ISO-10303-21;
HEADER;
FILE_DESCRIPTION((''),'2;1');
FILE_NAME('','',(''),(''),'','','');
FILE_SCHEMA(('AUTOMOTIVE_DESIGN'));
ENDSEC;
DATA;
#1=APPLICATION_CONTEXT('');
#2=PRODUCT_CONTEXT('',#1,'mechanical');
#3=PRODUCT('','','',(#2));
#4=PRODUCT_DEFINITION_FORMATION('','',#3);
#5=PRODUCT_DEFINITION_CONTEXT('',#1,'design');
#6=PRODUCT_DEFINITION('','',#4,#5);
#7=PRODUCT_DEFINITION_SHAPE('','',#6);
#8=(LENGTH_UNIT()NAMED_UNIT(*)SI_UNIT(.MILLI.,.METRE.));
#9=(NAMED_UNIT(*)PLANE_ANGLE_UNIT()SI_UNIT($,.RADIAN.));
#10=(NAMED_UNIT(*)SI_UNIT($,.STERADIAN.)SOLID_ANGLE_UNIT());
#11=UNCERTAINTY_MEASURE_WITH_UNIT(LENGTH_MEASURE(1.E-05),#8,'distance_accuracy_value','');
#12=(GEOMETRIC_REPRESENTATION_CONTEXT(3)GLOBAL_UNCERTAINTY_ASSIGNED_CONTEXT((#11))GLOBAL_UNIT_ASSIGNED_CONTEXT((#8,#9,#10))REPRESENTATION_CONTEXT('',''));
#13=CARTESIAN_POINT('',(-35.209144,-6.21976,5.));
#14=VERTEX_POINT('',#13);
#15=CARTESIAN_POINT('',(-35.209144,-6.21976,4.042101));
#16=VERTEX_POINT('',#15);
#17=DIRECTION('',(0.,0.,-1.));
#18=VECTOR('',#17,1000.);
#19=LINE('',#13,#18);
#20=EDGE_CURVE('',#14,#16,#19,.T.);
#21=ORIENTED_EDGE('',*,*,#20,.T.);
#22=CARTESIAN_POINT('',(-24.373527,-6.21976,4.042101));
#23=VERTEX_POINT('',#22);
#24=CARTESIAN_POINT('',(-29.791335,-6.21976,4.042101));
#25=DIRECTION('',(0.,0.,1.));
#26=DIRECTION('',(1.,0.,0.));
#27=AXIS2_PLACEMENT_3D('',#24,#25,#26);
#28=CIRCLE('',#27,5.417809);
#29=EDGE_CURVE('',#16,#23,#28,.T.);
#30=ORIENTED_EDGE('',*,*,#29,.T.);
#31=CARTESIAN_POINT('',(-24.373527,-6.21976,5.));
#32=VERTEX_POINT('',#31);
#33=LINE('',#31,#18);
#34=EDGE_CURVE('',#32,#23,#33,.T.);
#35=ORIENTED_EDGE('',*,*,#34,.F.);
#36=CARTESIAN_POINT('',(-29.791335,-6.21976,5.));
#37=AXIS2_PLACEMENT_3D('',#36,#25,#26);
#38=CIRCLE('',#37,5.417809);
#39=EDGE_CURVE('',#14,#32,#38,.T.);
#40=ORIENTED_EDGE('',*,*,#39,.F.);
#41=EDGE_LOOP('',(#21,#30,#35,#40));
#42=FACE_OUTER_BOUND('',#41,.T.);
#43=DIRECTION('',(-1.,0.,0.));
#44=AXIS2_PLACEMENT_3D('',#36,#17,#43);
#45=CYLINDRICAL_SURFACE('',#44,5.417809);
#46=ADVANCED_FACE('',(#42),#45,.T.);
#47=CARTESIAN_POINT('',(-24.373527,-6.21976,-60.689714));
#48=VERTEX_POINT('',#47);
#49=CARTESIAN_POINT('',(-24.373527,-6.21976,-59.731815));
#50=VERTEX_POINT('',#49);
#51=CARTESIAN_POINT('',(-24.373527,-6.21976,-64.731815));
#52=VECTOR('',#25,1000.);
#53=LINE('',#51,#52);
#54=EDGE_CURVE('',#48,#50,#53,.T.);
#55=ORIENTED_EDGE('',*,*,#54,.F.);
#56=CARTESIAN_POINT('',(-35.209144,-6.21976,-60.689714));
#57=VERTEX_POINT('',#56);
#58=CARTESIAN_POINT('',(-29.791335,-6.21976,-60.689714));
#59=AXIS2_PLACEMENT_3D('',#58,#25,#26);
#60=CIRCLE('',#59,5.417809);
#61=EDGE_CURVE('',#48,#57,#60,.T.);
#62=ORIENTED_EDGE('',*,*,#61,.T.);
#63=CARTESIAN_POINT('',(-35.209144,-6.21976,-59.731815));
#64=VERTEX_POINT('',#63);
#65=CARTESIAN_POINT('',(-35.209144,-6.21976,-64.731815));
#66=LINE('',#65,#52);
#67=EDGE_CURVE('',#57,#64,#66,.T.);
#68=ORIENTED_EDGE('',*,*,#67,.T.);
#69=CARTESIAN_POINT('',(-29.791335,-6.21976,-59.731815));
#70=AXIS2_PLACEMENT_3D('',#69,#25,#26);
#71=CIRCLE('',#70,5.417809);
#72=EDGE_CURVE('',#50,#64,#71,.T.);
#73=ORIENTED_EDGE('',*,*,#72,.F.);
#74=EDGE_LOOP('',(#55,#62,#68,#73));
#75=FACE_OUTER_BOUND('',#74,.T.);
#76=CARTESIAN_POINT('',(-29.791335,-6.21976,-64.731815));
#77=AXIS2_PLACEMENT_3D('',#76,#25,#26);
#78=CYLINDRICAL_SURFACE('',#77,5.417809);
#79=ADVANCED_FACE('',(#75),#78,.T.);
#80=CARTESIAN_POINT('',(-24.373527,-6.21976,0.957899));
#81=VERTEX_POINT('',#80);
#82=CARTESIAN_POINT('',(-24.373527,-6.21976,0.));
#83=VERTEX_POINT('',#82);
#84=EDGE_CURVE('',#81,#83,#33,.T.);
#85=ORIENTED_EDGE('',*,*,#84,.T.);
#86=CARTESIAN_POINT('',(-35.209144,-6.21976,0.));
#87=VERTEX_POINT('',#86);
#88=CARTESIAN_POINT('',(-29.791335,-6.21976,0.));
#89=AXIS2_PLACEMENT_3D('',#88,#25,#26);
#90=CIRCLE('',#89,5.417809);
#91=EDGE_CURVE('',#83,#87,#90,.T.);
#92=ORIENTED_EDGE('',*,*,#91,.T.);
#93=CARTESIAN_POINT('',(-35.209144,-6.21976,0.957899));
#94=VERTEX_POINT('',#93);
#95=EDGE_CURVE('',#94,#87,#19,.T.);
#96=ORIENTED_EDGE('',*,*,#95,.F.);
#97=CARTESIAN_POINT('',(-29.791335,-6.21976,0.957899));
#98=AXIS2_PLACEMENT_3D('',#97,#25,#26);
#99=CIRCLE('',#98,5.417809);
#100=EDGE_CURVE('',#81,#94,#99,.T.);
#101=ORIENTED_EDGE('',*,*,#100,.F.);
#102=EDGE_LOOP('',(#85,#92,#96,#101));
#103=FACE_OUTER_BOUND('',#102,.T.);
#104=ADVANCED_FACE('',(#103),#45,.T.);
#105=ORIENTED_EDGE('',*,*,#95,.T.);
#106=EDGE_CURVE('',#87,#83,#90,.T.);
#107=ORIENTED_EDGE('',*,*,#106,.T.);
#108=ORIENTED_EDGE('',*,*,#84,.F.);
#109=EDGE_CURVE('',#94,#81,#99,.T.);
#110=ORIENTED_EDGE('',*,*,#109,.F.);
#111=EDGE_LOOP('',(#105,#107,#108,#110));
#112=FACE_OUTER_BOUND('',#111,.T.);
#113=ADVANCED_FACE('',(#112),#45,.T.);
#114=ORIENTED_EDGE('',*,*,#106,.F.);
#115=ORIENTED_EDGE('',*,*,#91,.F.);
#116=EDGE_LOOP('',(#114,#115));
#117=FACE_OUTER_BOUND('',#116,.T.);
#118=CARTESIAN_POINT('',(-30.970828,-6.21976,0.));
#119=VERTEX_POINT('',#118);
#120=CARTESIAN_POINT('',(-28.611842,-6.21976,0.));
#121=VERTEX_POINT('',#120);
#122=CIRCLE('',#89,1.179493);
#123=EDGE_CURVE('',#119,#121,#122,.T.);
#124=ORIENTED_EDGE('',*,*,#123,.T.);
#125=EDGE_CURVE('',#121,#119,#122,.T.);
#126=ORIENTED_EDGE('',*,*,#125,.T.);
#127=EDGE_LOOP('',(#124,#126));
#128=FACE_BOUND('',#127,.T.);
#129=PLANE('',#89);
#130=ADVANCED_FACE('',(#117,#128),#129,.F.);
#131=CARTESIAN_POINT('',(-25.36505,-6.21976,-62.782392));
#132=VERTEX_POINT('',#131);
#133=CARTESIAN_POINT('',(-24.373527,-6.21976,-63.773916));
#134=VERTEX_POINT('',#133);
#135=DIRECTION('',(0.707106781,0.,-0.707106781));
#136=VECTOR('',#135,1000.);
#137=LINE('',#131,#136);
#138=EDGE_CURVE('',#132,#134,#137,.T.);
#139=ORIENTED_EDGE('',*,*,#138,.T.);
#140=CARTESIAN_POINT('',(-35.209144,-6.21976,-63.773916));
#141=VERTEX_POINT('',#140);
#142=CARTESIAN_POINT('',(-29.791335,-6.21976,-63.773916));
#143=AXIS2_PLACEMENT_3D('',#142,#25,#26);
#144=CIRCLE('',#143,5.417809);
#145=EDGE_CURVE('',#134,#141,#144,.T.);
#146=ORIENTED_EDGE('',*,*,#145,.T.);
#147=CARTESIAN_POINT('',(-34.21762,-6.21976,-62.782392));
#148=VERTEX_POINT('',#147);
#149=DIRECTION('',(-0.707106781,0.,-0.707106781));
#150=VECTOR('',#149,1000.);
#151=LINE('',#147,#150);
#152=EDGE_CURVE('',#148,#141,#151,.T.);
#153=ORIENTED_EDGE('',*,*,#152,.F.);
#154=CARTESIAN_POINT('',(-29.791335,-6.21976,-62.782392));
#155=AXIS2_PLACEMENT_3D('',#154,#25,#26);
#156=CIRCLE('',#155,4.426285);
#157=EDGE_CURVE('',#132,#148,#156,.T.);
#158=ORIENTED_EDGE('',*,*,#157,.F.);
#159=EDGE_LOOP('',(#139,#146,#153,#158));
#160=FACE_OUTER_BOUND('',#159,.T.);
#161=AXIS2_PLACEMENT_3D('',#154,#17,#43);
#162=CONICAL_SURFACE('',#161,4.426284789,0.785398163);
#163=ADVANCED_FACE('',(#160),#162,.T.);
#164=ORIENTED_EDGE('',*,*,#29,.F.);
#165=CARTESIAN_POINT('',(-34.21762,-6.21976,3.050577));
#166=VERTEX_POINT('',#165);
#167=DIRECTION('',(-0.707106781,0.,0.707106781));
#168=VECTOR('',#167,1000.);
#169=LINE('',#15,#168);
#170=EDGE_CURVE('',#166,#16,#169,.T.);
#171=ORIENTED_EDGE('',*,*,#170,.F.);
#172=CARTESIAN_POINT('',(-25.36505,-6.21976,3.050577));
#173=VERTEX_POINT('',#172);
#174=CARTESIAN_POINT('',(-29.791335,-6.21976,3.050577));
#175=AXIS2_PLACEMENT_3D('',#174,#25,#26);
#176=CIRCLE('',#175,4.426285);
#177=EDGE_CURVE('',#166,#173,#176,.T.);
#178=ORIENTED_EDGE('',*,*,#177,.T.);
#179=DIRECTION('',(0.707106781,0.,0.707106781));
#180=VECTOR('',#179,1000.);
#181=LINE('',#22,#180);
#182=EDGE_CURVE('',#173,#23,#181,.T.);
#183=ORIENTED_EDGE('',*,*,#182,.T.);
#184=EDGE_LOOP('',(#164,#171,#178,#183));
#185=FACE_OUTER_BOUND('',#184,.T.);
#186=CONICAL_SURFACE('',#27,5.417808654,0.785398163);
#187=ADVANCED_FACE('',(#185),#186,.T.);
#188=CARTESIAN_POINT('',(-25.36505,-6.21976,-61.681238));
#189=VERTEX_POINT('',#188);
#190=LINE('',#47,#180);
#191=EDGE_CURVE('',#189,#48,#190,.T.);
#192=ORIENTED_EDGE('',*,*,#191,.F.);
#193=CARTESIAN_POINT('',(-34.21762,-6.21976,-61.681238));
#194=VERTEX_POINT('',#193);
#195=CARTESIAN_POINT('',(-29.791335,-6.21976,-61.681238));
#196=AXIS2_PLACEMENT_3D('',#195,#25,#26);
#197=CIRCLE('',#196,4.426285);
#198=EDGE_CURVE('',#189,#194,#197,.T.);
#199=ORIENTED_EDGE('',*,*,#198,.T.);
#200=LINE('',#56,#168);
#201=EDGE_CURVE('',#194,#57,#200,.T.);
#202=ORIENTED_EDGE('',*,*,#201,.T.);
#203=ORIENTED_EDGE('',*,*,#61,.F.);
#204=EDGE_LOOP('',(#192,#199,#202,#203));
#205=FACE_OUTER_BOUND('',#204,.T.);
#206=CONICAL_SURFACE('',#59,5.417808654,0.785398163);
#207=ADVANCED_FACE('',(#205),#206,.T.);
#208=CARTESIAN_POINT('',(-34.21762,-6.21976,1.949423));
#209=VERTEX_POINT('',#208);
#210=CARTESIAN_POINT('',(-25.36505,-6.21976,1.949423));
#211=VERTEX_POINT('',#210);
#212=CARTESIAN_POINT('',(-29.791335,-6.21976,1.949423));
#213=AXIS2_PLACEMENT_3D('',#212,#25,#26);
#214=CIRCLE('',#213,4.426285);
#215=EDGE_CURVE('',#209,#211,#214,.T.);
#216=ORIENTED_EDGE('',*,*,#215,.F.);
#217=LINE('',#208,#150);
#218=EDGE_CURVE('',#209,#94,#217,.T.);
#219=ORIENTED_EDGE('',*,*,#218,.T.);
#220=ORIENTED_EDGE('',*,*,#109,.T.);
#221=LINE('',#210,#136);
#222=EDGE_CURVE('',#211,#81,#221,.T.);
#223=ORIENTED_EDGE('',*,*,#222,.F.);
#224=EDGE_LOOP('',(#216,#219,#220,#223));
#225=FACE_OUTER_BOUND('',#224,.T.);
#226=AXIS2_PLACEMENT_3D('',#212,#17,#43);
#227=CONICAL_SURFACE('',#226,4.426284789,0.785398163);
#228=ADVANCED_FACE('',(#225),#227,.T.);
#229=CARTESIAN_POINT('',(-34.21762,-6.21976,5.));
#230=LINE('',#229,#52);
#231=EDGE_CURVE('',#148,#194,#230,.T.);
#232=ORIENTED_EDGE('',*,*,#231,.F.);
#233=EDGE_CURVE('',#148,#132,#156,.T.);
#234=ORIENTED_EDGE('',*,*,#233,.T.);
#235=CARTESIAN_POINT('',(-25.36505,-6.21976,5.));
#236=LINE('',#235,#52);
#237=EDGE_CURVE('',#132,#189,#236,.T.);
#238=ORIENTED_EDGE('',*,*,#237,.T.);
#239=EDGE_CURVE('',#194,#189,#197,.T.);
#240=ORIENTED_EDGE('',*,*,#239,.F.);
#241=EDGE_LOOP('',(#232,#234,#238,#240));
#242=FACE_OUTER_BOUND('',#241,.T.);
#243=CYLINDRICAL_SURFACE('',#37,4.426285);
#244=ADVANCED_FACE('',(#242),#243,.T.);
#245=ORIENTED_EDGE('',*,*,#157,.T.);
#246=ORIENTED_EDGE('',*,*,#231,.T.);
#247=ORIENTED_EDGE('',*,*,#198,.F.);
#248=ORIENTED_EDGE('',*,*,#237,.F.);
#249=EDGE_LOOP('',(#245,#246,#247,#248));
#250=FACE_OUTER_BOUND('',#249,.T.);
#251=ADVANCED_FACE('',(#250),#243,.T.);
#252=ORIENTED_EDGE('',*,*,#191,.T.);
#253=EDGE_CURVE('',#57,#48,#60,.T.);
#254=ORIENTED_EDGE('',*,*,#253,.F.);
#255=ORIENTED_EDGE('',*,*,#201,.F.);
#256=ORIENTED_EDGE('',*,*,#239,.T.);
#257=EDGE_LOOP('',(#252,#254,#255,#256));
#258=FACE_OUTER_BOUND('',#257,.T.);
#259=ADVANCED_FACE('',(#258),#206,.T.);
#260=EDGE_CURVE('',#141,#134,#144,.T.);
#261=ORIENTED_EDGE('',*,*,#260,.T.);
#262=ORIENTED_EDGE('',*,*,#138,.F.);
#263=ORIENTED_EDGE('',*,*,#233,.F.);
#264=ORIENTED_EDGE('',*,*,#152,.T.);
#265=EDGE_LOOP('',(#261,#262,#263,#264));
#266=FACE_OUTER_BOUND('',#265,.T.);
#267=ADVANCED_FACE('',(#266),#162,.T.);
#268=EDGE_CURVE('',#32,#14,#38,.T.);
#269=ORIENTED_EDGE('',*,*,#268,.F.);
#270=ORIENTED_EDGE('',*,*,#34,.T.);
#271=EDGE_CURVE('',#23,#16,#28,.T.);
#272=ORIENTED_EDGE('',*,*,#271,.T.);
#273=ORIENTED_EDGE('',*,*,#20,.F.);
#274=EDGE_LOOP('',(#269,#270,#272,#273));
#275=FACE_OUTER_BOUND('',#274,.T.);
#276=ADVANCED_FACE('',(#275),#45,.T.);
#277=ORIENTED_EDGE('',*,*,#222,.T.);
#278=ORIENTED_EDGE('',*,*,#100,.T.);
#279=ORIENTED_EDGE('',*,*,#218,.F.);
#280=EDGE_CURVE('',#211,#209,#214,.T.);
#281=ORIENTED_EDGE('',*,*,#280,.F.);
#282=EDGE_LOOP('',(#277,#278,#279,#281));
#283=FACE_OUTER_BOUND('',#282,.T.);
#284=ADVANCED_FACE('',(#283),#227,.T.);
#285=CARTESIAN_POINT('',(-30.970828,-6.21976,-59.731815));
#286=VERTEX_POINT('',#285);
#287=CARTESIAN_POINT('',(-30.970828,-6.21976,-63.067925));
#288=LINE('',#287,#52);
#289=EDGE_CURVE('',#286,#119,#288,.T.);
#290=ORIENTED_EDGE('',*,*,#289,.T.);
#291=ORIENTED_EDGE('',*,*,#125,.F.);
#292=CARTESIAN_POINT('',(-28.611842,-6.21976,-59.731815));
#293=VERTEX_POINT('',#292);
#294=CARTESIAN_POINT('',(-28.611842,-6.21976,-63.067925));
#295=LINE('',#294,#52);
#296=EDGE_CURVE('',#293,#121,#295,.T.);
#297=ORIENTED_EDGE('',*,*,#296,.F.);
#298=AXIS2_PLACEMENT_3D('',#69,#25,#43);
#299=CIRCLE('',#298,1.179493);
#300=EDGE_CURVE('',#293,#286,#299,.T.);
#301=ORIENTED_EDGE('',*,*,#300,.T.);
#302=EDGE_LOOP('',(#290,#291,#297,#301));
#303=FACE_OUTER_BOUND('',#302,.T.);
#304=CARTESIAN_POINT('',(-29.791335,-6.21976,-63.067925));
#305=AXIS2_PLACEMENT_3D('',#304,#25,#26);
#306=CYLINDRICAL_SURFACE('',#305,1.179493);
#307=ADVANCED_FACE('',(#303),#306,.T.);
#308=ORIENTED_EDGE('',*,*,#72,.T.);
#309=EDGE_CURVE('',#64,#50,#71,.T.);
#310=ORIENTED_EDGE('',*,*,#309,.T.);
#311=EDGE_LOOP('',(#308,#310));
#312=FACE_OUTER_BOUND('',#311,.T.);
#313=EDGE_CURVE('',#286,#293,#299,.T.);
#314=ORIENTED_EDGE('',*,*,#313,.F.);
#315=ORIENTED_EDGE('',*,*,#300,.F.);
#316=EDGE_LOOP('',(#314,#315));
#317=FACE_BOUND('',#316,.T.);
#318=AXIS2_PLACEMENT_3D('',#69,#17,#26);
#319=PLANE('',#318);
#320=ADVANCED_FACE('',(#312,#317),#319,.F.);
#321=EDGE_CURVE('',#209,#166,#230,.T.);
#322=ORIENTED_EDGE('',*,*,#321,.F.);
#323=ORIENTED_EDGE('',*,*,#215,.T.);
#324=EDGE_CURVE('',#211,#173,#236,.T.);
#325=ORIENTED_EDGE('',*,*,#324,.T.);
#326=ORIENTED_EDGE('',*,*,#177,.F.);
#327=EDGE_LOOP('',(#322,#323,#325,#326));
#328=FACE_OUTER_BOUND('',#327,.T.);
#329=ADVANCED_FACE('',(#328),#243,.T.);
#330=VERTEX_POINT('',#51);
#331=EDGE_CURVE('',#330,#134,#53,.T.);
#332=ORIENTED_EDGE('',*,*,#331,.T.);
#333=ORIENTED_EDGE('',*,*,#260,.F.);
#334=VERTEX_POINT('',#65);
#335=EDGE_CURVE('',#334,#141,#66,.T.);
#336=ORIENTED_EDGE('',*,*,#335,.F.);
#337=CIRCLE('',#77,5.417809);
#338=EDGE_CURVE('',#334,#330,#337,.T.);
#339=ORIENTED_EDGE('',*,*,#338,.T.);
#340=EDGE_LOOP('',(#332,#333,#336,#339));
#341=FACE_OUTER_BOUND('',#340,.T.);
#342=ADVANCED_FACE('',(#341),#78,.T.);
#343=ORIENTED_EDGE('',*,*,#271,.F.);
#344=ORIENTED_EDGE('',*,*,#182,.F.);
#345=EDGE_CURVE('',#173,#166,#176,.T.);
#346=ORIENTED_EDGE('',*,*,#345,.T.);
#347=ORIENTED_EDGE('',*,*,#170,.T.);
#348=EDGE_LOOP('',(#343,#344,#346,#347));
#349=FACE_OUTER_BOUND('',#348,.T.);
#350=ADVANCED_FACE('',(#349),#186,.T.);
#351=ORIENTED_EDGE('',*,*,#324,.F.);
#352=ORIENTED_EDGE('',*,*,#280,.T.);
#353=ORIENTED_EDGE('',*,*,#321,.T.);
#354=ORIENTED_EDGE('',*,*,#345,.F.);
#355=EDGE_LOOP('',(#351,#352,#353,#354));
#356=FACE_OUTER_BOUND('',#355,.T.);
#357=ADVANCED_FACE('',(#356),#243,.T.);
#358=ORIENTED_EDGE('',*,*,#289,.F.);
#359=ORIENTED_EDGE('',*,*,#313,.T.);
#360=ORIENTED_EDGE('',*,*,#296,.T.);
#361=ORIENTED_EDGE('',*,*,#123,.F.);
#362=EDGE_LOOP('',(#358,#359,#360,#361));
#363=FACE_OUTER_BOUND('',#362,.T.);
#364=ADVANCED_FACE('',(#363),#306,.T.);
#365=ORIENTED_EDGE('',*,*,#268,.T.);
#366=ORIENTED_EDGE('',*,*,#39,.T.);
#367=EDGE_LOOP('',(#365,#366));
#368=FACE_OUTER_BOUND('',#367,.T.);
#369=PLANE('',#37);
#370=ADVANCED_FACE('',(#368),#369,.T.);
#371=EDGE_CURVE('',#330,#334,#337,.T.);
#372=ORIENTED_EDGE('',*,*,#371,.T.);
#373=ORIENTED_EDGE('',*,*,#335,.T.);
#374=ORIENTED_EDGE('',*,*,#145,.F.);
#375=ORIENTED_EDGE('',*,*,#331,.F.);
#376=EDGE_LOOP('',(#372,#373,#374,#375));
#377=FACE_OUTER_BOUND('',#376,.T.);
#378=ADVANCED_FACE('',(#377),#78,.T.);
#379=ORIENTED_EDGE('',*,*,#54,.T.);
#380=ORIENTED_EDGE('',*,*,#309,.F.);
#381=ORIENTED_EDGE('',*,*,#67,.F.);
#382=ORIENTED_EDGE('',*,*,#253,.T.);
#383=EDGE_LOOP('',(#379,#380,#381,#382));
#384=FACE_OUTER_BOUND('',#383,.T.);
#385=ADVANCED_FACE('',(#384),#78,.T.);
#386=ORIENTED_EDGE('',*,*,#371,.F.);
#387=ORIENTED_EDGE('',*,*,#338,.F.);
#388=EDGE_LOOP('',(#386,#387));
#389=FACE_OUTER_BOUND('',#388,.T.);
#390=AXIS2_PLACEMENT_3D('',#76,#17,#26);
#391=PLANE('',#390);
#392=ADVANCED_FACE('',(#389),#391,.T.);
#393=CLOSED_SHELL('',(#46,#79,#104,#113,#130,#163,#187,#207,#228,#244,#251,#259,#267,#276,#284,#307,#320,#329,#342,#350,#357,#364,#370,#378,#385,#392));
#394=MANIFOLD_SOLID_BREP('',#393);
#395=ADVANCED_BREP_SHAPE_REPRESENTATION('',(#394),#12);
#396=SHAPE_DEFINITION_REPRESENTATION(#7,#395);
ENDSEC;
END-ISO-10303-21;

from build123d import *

# Parameters (mm, degrees)
SKETCH1_R           = 1.179493096
BOSS_EXTRUDE1_DEPTH = 59.73181499
SKETCH2_R           = 5.417808654
BOSS_EXTRUDE2_DEPTH = 5


with BuildPart() as part:
    # Sketch1 → Boss-Extrude1 (new body)
    with BuildSketch(Plane.XY):
        with Locations((-29.791335202, -6.219759883)):
            Circle(SKETCH1_R)
    extrude(amount=-BOSS_EXTRUDE1_DEPTH)

    # Sketch2 → Boss-Extrude2 (add)
    with BuildSketch(Plane.XY):
        with Locations((-29.791335202, -6.219759883)):
            Circle(SKETCH2_R)
    boss_extrude2 = extrude(amount=BOSS_EXTRUDE2_DEPTH)

    # Mirror1: Boss-Extrude2 across plane
    add(boss_extrude2.mirror(Plane.XY.offset(-29.865907495)))

    # Sketch4 → Cut-Revolve2 (revolve, cut)
    with BuildSketch(Plane(origin=(0, -6.219759883, 0), x_dir=(0, 0, -1), z_dir=(0, 1, 0)), mode=Mode.PRIVATE) as cut_revolve2_sk:
        Polygon((-4.042100794, 35.209143856), (-3.05057693, 34.217619991), (-1.94942307, 34.217619991), (-0.957899206, 35.209143856), align=None)
        Polygon((60.689714196, 35.209143856), (61.68123806, 34.217619991), (62.78239192, 34.217619991), (63.773915784, 35.209143856), align=None)
    revolve(cut_revolve2_sk.sketch.rotate(Axis((-29.791335202, -6.219759883, 5), (0, 0, -1)), 180), axis=Axis((-29.791335202, -6.219759883, 5), (0, 0, -1)), mode=Mode.SUBTRACT)


solid = part.part
